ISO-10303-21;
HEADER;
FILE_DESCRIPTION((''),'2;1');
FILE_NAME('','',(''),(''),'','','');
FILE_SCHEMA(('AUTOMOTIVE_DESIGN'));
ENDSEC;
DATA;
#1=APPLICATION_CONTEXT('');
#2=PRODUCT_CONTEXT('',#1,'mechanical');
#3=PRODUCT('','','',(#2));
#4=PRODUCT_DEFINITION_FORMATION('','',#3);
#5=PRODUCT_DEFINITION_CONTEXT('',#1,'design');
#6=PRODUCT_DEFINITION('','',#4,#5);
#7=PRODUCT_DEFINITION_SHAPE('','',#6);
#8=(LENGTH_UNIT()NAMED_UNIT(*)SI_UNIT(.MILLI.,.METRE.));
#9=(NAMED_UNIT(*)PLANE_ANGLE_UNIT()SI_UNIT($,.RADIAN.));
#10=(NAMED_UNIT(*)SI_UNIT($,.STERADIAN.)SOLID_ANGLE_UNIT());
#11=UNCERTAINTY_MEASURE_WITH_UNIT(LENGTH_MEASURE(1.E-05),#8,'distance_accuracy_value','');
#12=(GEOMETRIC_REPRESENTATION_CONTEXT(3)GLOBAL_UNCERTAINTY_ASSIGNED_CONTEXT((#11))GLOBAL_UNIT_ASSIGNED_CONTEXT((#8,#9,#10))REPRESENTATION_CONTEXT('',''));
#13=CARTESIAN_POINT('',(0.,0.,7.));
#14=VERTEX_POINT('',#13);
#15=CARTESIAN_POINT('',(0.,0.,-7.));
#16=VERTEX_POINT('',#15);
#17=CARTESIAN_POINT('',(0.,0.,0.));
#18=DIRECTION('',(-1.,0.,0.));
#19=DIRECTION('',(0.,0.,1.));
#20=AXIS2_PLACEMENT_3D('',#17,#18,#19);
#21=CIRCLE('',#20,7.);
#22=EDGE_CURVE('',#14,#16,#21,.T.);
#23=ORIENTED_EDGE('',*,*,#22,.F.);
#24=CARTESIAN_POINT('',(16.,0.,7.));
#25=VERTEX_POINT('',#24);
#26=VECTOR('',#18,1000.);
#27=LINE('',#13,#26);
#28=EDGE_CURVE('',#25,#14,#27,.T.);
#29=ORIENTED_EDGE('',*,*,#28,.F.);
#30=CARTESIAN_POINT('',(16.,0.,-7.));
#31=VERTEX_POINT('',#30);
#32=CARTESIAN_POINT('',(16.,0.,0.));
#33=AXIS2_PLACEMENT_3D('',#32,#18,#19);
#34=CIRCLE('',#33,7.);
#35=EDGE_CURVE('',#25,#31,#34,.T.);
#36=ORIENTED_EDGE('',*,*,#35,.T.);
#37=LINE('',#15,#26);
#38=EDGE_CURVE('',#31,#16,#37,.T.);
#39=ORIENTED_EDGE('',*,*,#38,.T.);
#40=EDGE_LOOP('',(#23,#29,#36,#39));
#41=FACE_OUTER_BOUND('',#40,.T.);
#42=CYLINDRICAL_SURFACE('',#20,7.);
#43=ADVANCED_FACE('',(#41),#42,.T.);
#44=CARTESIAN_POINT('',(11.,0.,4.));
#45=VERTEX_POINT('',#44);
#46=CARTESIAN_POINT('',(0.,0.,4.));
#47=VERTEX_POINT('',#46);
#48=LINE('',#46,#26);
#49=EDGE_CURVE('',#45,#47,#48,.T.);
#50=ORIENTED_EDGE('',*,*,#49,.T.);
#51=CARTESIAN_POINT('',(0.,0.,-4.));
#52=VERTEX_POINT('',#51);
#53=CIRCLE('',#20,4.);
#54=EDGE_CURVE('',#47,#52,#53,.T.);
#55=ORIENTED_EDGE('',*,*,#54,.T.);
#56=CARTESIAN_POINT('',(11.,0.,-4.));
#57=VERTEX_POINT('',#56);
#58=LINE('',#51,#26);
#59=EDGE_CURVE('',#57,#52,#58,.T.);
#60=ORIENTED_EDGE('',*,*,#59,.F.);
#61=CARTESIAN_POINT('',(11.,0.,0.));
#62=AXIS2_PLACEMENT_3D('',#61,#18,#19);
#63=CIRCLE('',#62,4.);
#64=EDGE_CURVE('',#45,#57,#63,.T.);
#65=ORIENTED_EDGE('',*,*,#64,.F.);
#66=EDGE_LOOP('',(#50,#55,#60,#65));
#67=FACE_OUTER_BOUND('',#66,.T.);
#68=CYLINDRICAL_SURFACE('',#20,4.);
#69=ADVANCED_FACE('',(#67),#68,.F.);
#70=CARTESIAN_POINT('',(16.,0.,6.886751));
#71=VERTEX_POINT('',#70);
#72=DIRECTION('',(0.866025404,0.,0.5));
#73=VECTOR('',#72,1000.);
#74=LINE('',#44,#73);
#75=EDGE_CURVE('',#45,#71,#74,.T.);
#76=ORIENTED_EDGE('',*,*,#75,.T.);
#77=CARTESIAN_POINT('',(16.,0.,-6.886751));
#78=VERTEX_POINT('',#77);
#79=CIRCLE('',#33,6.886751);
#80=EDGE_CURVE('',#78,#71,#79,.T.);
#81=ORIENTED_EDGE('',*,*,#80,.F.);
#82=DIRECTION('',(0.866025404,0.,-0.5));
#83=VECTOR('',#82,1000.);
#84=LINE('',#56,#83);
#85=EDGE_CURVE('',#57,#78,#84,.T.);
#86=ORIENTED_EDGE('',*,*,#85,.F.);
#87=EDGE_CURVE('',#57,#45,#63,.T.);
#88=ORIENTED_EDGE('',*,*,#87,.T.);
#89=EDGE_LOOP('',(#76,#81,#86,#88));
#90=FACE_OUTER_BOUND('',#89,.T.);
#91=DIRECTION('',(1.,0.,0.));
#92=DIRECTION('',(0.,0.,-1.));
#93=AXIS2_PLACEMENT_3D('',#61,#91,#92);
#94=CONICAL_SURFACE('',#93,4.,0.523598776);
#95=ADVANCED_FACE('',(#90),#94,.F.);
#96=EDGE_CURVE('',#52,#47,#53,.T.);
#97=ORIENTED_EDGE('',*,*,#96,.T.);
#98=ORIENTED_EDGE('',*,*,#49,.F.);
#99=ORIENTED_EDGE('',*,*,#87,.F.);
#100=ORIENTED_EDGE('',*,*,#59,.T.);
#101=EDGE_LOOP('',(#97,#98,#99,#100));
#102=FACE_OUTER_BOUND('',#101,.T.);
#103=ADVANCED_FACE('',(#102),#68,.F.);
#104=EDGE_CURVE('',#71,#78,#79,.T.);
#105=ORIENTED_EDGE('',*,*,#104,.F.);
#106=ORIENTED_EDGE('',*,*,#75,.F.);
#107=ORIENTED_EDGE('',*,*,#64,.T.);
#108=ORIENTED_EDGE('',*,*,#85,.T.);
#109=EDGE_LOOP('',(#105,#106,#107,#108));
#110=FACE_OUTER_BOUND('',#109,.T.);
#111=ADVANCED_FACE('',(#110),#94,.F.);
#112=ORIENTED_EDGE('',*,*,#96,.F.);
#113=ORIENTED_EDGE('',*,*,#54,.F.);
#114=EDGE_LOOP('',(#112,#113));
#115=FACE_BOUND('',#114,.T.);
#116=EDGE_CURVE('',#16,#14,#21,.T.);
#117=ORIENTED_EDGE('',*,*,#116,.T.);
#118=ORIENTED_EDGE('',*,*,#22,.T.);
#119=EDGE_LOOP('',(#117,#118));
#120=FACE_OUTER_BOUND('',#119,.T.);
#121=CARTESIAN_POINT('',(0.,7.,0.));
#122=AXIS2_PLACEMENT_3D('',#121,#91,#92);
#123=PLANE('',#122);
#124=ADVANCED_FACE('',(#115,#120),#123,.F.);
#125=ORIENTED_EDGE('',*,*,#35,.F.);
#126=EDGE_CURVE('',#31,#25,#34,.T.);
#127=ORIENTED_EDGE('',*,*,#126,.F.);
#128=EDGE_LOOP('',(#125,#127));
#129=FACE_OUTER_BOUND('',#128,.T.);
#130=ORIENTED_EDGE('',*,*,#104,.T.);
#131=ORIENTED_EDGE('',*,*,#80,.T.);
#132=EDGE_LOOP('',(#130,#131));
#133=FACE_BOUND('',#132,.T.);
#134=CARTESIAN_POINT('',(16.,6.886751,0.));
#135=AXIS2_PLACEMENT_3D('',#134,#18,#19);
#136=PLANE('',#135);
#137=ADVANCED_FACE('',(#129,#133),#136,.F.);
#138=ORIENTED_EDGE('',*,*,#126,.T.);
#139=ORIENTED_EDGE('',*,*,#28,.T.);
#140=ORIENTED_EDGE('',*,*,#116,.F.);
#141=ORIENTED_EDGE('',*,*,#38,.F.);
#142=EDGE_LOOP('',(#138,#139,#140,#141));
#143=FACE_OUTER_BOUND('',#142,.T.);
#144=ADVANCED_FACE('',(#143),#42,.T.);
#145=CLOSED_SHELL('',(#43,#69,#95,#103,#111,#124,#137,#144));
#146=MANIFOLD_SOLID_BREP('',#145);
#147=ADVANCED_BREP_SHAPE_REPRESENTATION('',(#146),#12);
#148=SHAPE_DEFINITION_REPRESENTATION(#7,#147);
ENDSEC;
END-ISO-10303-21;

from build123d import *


with BuildPart() as part:
    # Sketch1 → Revolve1 (revolve)
    with BuildSketch(Plane.XY, mode=Mode.PRIVATE) as revolve1_sk:
        Polygon((0, 4), (11, 4), (16, 6.886751346), (16, 7), (0, 7), align=None)
    revolve(revolve1_sk.sketch.rotate(Axis((0, 0, 0), (1, 0, 0)), 90), axis=Axis((0, 0, 0), (1, 0, 0)))


solid = part.part
